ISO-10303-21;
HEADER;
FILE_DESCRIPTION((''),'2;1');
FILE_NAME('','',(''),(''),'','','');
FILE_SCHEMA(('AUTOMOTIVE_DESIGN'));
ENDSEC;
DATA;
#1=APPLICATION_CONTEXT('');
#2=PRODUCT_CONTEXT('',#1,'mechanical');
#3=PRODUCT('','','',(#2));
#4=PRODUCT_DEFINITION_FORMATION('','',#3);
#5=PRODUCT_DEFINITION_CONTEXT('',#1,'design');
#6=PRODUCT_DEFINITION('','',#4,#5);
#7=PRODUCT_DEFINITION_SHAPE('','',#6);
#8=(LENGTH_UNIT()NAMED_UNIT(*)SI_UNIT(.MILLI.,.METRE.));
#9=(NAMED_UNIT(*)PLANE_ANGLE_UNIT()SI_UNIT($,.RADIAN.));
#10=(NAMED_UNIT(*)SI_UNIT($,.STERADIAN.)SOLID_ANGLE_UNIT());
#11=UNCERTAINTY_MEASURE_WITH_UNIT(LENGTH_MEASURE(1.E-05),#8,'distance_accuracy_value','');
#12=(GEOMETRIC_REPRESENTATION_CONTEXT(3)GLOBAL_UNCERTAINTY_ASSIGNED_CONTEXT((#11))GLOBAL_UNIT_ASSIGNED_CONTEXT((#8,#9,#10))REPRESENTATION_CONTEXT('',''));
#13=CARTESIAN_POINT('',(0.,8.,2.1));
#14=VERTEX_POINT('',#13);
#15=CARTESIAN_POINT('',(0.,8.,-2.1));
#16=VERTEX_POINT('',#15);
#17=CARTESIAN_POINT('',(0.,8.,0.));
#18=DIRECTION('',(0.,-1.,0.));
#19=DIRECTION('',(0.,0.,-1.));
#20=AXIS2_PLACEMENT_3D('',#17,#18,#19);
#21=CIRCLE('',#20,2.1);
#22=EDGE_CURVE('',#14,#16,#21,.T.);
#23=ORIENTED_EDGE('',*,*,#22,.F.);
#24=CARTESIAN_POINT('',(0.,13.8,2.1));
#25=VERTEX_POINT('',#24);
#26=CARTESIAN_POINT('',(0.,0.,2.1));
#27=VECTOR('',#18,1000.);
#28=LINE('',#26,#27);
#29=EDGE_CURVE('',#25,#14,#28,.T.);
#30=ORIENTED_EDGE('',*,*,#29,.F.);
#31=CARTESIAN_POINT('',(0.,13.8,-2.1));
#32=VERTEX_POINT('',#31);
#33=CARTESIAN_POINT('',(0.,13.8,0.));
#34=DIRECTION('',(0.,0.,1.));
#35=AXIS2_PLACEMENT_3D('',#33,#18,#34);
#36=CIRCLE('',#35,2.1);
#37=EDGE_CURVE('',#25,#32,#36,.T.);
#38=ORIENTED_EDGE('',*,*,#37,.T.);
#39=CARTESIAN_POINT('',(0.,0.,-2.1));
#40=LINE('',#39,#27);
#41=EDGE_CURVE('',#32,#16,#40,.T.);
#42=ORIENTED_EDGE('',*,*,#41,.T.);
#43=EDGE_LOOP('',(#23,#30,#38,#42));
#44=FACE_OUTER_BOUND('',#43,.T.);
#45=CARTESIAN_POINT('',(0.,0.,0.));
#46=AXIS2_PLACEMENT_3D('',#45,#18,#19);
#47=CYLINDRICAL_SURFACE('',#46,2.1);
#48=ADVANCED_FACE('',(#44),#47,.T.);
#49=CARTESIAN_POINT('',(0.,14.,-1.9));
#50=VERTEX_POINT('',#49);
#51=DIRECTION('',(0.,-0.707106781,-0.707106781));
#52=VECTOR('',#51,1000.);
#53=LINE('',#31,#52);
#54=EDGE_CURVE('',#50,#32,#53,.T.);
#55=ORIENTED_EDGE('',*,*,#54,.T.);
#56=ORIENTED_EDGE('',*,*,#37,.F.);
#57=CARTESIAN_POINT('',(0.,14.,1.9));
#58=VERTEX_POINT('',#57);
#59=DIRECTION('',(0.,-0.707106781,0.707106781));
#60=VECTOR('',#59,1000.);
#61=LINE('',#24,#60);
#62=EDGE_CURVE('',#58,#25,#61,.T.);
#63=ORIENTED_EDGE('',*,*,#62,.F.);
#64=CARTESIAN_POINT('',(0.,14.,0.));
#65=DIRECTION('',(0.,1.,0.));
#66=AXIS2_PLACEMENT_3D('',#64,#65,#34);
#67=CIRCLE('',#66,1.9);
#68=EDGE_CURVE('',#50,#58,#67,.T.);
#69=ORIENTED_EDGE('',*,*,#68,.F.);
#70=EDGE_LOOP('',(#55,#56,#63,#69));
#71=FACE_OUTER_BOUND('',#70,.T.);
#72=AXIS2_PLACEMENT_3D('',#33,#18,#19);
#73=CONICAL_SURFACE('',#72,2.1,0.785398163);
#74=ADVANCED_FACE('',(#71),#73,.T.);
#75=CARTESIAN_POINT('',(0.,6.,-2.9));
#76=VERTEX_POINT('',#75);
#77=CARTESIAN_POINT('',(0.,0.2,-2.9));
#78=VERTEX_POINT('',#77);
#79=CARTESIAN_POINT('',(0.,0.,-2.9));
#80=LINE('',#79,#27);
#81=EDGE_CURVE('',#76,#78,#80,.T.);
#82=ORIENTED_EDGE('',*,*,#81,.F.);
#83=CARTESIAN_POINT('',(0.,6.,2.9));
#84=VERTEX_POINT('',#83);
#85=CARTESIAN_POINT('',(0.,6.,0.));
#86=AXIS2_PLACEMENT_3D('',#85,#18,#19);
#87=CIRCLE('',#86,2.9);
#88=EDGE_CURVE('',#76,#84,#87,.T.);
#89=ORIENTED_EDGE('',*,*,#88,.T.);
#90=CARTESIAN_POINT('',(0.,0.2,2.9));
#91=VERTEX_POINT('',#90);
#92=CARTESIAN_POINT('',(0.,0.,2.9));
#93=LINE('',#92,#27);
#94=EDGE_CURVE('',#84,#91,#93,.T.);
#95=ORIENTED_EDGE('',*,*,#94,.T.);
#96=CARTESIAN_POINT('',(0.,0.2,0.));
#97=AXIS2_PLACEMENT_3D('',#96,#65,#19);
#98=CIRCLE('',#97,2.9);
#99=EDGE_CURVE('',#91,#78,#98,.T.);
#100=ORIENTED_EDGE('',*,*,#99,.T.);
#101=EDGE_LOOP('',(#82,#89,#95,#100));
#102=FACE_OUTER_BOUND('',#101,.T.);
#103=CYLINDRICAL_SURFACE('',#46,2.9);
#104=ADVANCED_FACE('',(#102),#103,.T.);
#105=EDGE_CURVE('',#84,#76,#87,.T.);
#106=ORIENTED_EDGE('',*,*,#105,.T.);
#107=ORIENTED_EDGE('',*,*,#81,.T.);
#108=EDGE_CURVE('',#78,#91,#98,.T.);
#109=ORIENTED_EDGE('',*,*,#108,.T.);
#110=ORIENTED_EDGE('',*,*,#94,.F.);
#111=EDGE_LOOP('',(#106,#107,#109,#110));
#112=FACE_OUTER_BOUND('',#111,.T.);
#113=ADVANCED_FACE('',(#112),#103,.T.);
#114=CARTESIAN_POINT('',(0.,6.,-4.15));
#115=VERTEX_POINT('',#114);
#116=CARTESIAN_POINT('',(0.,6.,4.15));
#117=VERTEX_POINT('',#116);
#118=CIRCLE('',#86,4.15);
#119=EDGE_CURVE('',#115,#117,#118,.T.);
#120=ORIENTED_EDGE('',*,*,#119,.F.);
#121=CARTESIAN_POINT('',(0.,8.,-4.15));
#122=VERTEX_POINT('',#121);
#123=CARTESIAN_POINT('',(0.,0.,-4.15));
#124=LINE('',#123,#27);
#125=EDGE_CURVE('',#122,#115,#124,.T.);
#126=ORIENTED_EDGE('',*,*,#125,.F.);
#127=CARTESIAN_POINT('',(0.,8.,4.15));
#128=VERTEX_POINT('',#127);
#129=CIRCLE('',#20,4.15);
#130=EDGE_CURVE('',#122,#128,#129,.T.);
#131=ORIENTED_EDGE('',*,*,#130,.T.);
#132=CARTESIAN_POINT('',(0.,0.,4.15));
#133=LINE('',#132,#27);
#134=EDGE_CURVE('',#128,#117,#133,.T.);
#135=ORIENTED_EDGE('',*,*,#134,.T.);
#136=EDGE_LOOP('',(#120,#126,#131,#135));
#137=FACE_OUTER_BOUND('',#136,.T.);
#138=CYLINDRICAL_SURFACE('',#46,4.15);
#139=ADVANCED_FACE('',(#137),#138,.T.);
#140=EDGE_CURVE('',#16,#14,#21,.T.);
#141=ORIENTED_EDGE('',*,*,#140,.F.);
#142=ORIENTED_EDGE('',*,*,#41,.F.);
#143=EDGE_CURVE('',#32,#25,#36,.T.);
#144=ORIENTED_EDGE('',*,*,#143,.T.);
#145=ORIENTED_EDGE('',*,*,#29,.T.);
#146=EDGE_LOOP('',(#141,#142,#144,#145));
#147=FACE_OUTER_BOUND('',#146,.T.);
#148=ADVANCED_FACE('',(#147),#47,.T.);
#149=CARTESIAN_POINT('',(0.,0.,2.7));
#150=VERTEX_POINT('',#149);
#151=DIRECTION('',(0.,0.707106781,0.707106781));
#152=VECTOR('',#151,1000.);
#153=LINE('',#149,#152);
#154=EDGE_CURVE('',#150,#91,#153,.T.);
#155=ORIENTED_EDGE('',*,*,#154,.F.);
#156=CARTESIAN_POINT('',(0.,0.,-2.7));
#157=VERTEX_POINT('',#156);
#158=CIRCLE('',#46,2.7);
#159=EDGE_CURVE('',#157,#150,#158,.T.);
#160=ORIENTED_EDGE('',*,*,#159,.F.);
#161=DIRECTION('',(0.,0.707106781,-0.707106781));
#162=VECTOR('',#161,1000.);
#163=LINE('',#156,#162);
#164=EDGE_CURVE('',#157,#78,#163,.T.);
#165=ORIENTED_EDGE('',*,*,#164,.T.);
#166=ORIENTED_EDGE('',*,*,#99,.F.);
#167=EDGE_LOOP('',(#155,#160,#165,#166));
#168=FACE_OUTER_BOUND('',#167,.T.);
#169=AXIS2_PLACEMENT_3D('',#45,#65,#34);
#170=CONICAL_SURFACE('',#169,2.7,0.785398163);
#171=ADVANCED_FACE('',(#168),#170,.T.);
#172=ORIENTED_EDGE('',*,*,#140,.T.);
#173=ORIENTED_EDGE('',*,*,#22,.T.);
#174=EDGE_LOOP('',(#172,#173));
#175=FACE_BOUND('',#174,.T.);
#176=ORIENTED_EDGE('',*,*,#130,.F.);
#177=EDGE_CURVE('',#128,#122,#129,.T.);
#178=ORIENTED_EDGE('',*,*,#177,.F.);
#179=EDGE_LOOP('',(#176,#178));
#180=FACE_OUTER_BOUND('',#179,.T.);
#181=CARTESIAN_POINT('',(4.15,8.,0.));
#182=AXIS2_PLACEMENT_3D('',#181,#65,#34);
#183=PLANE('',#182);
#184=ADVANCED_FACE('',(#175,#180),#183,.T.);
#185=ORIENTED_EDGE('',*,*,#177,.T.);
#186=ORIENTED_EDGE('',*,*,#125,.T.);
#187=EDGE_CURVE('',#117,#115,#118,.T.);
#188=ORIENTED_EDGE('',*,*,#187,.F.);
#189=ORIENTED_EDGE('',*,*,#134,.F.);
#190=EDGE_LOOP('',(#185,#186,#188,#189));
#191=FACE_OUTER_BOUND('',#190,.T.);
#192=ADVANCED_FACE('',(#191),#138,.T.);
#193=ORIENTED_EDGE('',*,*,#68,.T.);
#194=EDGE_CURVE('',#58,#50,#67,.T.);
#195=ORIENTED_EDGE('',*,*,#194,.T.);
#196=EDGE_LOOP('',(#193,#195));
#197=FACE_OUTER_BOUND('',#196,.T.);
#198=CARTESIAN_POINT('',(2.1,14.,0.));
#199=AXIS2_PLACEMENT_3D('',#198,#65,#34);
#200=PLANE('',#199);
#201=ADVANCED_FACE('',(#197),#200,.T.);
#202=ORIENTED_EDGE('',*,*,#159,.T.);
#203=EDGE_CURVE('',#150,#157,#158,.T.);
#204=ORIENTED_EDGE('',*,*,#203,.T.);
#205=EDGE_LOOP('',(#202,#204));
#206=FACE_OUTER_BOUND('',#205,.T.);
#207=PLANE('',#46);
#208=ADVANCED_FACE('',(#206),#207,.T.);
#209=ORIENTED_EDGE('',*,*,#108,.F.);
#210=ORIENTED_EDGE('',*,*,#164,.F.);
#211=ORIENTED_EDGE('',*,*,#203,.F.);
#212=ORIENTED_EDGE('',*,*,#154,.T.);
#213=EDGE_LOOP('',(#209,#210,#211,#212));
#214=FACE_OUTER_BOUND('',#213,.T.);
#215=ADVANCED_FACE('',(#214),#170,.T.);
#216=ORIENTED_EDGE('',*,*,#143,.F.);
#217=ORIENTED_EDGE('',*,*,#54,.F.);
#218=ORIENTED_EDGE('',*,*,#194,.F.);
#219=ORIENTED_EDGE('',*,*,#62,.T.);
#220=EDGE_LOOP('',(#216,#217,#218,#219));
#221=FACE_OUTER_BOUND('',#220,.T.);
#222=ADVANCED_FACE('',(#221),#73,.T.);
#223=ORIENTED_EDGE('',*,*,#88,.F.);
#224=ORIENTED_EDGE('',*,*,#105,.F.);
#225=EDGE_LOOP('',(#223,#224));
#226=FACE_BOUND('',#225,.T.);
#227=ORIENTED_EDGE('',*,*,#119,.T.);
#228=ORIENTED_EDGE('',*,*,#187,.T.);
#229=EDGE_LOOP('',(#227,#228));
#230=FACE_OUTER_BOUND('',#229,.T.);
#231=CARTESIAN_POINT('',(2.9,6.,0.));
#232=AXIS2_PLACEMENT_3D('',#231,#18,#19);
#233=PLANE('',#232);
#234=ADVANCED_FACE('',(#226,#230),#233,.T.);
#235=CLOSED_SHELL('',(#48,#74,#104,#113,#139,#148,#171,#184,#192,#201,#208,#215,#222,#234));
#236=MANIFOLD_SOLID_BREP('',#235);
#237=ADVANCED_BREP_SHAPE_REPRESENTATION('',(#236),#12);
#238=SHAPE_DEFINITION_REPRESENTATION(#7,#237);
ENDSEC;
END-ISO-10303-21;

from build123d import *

# Parameters (mm, degrees)
CHAMFER1_SIZE = 0.2


with BuildPart() as part:
    # Sketch1 → Revolve1 (revolve)
    with BuildSketch(Plane.XY, mode=Mode.PRIVATE) as revolve1_sk:
        Polygon((0, 0), (0, 14), (2.1, 14), (2.1, 8), (4.15, 8), (4.15, 6), (2.9, 6), (2.9, 0), align=None)
    revolve(revolve1_sk.sketch.rotate(Axis((0, 0, 0), (0, 1, 0)), 90), axis=Axis((0, 0, 0), (0, 1, 0)))

    # Chamfer1
    chamfer1_edges = [part.edges().sort_by_distance(p)[0] for p in [
        (0, 14, 2.1),
        (0, 0, 2.9),
    ]]
    chamfer(chamfer1_edges, length=CHAMFER1_SIZE)


solid = part.part
